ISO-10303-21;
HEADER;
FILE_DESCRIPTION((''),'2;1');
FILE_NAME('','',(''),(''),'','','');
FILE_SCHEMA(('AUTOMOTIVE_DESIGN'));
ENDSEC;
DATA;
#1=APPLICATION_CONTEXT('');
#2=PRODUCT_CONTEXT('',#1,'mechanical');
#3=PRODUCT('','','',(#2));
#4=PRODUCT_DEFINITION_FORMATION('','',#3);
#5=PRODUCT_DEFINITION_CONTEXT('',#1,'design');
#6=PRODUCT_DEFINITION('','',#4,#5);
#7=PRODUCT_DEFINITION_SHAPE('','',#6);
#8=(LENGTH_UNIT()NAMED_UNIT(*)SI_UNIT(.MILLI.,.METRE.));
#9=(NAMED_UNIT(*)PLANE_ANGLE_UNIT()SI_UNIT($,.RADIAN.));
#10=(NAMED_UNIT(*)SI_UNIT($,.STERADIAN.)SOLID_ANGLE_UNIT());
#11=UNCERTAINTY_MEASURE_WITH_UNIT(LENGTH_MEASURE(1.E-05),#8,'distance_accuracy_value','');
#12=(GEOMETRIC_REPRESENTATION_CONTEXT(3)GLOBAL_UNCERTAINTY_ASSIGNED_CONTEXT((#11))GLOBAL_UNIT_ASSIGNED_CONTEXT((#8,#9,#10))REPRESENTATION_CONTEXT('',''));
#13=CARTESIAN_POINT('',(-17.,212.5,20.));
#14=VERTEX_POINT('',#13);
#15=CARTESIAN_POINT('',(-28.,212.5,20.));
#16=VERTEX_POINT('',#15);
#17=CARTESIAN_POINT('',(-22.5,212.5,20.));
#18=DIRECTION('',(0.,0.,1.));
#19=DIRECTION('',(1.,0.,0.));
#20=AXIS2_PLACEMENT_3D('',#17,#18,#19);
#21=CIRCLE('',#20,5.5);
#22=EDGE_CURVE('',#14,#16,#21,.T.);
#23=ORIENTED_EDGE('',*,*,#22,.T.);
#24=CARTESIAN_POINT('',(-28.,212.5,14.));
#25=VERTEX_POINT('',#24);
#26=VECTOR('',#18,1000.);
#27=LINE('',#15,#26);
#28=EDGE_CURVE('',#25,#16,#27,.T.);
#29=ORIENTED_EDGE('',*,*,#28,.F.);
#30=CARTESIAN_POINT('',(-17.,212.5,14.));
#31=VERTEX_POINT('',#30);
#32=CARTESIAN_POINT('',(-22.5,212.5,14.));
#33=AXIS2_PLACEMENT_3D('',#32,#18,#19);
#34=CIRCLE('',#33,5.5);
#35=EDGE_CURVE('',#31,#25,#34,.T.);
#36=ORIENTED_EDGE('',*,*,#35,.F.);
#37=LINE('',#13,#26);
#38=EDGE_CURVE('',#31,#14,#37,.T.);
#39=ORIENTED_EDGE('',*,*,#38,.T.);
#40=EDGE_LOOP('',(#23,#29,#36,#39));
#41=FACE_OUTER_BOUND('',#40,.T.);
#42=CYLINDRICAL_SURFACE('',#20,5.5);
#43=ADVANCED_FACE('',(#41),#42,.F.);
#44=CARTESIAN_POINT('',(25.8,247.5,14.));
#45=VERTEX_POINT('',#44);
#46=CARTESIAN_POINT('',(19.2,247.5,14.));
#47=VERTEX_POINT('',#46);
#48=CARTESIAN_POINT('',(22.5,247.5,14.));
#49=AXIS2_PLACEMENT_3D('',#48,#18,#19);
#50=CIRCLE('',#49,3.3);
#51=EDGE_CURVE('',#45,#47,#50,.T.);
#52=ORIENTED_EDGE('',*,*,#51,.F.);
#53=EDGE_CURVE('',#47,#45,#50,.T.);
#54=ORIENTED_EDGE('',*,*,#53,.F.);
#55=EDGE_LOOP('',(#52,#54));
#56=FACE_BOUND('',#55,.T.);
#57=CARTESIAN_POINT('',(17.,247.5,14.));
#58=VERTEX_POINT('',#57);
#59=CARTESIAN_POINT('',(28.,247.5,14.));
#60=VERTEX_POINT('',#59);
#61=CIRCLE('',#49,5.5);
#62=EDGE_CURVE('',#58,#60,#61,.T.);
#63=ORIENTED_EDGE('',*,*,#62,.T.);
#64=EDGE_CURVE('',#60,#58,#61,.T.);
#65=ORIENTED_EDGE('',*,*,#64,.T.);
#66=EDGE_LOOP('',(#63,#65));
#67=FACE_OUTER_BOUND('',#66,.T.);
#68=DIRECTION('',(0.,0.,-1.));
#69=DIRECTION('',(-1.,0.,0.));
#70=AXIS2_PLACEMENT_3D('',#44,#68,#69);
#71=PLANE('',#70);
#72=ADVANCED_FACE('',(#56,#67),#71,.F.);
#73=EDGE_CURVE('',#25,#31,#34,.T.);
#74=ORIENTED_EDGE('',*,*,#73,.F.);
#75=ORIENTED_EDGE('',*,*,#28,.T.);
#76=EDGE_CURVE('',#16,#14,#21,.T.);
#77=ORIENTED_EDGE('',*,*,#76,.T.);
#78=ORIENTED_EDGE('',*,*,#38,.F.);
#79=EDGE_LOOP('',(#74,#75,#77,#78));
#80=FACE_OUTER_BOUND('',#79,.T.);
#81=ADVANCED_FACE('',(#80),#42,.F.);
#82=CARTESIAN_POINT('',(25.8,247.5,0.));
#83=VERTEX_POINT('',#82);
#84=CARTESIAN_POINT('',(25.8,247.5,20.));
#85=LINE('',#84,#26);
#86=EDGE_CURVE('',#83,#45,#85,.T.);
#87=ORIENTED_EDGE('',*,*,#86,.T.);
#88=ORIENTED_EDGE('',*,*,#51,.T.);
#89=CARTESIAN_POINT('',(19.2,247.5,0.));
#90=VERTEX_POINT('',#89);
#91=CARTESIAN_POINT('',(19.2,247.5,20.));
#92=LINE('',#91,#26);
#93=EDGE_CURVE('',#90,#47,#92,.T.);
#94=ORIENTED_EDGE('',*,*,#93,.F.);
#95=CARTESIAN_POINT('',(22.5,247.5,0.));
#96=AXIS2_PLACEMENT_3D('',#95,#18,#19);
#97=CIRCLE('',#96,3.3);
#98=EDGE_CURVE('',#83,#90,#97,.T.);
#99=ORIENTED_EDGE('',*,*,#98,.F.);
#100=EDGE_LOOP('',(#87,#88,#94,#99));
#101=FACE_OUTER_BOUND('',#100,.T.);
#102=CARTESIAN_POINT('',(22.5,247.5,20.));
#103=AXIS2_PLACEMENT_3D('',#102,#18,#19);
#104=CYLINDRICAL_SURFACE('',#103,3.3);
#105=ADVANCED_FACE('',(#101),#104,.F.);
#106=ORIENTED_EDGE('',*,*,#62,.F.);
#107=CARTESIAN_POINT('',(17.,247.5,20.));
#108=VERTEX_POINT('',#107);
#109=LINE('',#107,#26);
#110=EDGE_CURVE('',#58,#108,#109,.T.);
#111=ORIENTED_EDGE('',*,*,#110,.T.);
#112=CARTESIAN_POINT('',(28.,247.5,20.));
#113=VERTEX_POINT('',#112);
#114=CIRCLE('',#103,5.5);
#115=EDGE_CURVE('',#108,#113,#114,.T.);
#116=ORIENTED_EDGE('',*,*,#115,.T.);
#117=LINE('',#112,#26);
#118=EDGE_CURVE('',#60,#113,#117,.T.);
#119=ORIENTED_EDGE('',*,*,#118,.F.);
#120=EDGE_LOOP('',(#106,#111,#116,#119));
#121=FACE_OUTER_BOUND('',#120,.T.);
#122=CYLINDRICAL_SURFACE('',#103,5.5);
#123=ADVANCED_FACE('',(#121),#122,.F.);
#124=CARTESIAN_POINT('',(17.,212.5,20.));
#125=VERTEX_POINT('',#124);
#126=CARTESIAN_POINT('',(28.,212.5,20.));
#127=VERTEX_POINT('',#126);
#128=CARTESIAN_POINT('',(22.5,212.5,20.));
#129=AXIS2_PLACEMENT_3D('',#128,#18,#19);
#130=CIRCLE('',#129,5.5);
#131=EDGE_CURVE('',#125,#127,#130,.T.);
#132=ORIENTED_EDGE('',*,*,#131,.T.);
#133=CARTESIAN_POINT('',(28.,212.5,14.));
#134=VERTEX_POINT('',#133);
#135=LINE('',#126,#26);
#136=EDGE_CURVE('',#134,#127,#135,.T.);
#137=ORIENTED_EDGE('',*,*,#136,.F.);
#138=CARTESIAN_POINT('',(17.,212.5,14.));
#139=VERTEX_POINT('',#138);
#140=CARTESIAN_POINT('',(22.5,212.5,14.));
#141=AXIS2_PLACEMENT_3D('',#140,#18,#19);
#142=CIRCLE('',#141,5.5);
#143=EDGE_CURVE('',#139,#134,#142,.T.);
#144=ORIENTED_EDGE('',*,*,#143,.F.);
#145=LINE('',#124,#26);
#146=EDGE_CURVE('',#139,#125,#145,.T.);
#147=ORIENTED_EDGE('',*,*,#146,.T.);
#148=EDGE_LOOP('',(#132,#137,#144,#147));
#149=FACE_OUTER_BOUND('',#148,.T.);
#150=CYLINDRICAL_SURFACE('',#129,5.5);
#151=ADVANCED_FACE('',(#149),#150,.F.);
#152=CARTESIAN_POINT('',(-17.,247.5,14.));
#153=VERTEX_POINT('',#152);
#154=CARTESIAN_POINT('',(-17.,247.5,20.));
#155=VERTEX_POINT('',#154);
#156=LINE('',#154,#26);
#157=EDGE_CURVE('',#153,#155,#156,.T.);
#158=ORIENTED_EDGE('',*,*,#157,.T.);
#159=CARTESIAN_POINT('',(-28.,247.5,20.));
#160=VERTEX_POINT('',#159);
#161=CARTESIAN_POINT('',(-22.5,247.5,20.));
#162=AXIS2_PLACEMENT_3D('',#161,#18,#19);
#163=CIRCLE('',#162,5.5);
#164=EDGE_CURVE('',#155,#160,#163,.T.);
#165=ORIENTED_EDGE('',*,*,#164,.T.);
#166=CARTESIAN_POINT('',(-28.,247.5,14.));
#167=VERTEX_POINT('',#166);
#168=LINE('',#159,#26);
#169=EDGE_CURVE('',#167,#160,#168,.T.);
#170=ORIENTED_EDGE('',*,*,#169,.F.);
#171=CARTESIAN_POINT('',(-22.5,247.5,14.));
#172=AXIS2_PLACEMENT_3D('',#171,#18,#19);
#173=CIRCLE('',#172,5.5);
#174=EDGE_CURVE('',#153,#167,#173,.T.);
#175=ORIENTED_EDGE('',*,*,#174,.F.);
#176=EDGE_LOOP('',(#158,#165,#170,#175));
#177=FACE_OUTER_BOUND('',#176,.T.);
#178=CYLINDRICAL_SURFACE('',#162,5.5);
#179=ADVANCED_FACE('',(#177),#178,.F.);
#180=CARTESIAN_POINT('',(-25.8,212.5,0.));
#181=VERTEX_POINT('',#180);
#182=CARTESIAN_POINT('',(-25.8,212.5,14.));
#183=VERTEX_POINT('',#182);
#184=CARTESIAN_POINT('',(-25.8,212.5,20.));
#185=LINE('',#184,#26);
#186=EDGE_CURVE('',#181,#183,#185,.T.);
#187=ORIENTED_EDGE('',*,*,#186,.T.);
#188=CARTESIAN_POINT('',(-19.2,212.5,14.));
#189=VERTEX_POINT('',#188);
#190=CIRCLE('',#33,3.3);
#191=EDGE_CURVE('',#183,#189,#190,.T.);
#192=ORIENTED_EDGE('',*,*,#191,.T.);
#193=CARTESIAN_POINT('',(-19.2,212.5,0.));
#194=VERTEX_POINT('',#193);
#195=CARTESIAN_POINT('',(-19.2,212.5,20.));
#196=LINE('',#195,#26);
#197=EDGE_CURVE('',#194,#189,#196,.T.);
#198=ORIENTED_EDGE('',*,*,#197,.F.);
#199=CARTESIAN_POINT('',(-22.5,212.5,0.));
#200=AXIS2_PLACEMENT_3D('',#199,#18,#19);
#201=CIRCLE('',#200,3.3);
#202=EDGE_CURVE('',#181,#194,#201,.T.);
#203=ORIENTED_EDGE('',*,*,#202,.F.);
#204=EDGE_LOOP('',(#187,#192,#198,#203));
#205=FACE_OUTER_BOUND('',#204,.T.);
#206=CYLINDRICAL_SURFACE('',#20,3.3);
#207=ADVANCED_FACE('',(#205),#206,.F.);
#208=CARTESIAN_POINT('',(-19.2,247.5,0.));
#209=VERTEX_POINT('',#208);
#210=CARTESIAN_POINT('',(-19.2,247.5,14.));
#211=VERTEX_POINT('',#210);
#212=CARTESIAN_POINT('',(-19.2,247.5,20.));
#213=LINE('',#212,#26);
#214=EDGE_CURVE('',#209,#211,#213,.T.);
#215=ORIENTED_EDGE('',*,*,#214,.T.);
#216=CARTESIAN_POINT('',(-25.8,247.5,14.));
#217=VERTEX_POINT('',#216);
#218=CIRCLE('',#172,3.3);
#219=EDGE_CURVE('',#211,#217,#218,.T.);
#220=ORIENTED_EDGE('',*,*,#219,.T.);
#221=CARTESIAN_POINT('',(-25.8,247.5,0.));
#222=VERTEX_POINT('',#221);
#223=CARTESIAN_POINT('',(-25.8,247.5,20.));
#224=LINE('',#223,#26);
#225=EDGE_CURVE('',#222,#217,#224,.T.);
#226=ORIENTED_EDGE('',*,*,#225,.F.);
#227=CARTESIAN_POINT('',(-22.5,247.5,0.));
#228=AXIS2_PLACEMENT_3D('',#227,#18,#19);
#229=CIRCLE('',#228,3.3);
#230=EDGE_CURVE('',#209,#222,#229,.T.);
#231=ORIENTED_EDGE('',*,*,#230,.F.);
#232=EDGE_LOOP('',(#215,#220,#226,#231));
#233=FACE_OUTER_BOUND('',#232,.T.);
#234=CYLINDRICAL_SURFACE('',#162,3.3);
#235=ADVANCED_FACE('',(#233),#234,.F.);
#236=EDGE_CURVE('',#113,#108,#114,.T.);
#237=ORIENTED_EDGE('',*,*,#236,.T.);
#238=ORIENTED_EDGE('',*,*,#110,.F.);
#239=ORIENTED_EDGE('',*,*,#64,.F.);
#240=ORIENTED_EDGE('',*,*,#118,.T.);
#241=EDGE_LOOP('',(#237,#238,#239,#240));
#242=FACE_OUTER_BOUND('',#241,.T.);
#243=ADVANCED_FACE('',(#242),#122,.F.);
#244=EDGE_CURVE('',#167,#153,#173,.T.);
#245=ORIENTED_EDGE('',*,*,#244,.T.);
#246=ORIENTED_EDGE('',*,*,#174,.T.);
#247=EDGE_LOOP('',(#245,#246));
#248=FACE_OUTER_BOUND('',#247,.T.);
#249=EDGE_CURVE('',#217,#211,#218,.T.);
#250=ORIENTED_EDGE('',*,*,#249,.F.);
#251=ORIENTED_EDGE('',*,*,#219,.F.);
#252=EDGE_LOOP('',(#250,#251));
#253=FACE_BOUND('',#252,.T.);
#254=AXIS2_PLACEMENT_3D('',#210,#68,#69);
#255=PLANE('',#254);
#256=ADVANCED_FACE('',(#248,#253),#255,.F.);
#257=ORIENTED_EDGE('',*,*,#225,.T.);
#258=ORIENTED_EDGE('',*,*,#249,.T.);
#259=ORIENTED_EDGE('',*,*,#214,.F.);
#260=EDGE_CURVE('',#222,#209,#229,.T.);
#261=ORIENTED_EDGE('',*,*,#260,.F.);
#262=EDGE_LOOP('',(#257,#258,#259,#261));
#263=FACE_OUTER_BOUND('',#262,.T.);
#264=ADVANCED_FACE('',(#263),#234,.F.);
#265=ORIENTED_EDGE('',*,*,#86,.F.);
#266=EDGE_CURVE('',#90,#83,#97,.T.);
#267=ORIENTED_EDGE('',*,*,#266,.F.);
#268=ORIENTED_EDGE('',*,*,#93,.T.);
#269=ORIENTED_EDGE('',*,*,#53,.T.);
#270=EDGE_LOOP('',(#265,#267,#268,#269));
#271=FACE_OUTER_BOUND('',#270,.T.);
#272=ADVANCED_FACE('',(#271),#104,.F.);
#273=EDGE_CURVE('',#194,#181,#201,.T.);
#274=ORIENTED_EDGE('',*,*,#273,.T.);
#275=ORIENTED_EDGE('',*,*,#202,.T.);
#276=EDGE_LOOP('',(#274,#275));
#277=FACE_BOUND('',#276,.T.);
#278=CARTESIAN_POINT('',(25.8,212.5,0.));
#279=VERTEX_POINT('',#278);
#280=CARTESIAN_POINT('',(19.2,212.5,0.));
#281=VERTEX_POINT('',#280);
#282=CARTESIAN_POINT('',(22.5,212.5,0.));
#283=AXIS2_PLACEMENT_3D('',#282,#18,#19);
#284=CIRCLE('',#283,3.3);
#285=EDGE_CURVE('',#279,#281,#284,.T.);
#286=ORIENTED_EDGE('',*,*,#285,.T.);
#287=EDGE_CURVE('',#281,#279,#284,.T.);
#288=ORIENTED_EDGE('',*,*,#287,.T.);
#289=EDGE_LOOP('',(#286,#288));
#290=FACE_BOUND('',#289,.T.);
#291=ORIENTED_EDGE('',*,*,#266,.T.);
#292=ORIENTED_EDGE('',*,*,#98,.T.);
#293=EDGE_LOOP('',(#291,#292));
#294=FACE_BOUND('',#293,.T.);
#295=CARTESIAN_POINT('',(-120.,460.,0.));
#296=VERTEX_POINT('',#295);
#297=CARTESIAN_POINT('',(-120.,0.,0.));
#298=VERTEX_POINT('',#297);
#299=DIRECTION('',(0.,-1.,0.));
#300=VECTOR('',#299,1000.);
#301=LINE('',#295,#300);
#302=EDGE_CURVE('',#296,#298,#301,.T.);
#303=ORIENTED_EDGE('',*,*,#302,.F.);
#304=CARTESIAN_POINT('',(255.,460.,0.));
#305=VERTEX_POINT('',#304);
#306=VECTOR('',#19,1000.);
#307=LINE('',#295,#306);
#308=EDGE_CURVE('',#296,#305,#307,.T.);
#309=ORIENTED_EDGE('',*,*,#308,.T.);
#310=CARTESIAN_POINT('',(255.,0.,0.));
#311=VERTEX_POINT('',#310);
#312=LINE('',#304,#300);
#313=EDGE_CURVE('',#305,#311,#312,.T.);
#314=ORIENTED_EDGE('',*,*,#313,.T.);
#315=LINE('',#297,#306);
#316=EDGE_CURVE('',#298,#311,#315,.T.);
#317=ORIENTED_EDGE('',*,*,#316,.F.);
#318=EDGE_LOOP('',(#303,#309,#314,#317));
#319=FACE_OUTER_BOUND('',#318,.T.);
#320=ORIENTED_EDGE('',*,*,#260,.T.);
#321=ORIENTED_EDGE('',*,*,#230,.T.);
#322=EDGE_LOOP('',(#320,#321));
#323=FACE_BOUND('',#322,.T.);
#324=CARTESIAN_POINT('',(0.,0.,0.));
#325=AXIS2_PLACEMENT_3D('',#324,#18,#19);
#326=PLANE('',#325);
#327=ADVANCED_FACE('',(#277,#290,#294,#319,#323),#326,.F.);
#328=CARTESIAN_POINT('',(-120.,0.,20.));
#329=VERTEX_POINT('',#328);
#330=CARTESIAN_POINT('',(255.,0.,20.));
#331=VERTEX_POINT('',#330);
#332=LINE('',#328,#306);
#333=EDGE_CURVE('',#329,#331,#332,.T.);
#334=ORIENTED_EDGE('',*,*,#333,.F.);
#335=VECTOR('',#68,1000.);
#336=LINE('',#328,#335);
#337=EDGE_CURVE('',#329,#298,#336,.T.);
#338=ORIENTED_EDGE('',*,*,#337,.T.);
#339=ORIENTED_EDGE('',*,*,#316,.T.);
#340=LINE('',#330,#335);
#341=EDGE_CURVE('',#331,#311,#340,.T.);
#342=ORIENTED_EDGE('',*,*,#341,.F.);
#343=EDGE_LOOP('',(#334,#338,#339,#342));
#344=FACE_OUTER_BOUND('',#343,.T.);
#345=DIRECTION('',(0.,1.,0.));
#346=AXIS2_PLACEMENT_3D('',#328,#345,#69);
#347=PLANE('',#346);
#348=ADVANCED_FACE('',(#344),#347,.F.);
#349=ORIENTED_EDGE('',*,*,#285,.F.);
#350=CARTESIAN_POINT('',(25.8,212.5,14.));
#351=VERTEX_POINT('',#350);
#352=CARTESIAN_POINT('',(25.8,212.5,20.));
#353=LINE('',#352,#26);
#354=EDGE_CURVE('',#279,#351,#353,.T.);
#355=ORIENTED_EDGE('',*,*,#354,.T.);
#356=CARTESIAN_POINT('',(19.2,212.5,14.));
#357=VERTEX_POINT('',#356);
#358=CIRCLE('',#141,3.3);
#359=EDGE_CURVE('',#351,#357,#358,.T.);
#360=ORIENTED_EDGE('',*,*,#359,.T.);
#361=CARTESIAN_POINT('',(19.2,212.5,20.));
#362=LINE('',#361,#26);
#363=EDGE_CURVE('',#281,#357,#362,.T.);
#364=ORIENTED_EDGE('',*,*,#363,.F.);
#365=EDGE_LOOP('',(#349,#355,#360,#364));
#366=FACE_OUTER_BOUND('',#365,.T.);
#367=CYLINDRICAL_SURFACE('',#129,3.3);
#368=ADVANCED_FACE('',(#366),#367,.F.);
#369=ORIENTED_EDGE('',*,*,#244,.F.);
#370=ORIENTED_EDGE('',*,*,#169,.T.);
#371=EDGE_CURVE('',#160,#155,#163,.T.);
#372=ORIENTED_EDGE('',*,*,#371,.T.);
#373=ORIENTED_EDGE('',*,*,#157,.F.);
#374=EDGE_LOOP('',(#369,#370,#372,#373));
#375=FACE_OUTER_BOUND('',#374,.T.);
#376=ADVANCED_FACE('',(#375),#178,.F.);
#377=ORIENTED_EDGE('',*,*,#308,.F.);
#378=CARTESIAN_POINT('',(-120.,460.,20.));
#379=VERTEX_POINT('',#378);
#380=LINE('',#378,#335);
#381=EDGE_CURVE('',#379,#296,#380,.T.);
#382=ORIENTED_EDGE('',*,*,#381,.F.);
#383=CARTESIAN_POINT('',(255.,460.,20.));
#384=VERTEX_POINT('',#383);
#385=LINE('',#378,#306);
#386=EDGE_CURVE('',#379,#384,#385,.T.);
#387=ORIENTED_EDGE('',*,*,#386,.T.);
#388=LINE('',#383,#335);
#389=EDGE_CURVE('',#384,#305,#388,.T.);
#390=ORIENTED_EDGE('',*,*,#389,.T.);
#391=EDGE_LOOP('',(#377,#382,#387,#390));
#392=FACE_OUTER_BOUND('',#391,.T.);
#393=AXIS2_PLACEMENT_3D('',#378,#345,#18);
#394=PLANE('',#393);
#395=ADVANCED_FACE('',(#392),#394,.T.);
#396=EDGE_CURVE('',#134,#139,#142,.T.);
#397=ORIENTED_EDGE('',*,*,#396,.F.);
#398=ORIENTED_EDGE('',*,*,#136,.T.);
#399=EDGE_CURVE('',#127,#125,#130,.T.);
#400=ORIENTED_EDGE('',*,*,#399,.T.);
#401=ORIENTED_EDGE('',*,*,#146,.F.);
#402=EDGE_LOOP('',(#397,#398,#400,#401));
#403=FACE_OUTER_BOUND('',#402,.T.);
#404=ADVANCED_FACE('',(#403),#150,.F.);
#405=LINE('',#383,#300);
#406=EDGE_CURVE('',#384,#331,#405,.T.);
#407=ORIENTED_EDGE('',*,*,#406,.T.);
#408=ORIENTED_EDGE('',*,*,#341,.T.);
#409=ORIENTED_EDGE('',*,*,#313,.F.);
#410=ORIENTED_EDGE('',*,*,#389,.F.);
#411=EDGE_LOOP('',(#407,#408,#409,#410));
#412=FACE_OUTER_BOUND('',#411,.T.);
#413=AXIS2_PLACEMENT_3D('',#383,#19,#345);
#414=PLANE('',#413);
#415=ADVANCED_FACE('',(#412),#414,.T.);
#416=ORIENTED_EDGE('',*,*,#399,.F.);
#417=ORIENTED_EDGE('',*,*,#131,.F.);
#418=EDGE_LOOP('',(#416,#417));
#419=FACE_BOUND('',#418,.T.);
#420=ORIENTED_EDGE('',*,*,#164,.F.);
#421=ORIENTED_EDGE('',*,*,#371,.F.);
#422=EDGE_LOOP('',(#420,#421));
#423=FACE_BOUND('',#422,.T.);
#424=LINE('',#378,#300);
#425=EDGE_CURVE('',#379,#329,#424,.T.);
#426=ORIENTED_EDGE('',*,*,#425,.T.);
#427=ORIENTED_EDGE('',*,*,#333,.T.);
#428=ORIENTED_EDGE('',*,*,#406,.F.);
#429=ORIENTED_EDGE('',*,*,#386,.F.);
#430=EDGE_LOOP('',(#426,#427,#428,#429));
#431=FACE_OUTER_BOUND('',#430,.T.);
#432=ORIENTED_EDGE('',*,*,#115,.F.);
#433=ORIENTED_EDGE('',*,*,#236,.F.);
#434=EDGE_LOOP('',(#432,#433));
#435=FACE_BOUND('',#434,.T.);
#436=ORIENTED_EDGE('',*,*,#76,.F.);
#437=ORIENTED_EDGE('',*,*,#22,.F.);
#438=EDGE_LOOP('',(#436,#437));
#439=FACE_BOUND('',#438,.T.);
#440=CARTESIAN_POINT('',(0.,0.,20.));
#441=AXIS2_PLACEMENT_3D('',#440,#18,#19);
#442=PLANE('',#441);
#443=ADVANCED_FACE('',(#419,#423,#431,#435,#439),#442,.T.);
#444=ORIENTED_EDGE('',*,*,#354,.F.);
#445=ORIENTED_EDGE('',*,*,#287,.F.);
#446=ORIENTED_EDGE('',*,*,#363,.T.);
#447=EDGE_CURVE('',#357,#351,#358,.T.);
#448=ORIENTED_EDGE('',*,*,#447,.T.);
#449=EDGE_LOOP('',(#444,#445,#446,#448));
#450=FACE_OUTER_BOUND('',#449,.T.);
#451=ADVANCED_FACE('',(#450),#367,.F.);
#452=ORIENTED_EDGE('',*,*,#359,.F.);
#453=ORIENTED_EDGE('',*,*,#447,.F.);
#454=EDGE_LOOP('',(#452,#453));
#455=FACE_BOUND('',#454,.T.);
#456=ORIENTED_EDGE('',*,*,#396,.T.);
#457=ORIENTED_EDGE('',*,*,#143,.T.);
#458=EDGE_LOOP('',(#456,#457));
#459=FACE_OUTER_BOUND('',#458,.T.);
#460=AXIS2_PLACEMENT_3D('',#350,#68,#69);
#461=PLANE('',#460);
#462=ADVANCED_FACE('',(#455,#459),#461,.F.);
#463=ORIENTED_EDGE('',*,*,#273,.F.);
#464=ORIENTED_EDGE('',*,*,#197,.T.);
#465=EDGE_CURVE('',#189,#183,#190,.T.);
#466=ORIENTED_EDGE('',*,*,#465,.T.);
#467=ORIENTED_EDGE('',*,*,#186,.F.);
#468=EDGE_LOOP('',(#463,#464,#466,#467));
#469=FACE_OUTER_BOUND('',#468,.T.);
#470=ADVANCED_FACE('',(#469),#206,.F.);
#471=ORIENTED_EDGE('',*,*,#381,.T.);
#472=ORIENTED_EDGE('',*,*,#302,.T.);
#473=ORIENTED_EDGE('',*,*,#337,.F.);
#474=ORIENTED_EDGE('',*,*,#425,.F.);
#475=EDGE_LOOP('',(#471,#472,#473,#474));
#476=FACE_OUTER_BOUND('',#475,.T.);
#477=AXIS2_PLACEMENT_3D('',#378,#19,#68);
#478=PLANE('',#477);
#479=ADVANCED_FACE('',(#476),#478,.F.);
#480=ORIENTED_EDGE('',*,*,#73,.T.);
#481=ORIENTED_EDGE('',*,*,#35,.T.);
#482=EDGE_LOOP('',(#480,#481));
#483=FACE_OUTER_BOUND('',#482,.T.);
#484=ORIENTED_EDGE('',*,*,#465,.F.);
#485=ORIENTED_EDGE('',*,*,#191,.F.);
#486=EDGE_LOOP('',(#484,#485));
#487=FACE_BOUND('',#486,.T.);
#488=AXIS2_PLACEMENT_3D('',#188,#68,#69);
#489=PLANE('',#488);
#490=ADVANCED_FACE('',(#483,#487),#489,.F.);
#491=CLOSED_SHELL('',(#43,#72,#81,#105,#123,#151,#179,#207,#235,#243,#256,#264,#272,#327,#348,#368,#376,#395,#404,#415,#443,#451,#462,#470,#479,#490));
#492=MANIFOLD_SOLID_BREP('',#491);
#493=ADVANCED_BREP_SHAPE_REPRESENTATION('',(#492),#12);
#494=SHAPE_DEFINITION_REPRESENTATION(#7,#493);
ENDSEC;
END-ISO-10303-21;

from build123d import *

# Parameters (mm, degrees)
SKETCH1_W                               = 375
SKETCH1_H                               = 460
BOSS_EXTRUDE1_DEPTH                     = 20
CBORE_FOR_M6_HEX_HEAD_BOLT1_D           = 6.6
CBORE_FOR_M6_HEX_HEAD_BOLT1_CBORE_D     = 11
CBORE_FOR_M6_HEX_HEAD_BOLT1_CBORE_DEPTH = 6


with BuildPart() as part:
    # Sketch1 → Boss-Extrude1 (new body)
    with BuildSketch(Plane.XY):
        with Locations((67.5, 230)):
            Rectangle(SKETCH1_W, SKETCH1_H)
    extrude(amount=BOSS_EXTRUDE1_DEPTH)

    # CBORE for M6 Hex Head Bolt1 (through all)
    with Locations(Plane.XY.offset(20)):
        with Locations((-22.5, 247.5), (22.5, 247.5), (22.5, 212.5), (-22.5, 212.5)):
            CounterBoreHole(CBORE_FOR_M6_HEX_HEAD_BOLT1_D / 2, CBORE_FOR_M6_HEX_HEAD_BOLT1_CBORE_D / 2, CBORE_FOR_M6_HEX_HEAD_BOLT1_CBORE_DEPTH)


solid = part.part
